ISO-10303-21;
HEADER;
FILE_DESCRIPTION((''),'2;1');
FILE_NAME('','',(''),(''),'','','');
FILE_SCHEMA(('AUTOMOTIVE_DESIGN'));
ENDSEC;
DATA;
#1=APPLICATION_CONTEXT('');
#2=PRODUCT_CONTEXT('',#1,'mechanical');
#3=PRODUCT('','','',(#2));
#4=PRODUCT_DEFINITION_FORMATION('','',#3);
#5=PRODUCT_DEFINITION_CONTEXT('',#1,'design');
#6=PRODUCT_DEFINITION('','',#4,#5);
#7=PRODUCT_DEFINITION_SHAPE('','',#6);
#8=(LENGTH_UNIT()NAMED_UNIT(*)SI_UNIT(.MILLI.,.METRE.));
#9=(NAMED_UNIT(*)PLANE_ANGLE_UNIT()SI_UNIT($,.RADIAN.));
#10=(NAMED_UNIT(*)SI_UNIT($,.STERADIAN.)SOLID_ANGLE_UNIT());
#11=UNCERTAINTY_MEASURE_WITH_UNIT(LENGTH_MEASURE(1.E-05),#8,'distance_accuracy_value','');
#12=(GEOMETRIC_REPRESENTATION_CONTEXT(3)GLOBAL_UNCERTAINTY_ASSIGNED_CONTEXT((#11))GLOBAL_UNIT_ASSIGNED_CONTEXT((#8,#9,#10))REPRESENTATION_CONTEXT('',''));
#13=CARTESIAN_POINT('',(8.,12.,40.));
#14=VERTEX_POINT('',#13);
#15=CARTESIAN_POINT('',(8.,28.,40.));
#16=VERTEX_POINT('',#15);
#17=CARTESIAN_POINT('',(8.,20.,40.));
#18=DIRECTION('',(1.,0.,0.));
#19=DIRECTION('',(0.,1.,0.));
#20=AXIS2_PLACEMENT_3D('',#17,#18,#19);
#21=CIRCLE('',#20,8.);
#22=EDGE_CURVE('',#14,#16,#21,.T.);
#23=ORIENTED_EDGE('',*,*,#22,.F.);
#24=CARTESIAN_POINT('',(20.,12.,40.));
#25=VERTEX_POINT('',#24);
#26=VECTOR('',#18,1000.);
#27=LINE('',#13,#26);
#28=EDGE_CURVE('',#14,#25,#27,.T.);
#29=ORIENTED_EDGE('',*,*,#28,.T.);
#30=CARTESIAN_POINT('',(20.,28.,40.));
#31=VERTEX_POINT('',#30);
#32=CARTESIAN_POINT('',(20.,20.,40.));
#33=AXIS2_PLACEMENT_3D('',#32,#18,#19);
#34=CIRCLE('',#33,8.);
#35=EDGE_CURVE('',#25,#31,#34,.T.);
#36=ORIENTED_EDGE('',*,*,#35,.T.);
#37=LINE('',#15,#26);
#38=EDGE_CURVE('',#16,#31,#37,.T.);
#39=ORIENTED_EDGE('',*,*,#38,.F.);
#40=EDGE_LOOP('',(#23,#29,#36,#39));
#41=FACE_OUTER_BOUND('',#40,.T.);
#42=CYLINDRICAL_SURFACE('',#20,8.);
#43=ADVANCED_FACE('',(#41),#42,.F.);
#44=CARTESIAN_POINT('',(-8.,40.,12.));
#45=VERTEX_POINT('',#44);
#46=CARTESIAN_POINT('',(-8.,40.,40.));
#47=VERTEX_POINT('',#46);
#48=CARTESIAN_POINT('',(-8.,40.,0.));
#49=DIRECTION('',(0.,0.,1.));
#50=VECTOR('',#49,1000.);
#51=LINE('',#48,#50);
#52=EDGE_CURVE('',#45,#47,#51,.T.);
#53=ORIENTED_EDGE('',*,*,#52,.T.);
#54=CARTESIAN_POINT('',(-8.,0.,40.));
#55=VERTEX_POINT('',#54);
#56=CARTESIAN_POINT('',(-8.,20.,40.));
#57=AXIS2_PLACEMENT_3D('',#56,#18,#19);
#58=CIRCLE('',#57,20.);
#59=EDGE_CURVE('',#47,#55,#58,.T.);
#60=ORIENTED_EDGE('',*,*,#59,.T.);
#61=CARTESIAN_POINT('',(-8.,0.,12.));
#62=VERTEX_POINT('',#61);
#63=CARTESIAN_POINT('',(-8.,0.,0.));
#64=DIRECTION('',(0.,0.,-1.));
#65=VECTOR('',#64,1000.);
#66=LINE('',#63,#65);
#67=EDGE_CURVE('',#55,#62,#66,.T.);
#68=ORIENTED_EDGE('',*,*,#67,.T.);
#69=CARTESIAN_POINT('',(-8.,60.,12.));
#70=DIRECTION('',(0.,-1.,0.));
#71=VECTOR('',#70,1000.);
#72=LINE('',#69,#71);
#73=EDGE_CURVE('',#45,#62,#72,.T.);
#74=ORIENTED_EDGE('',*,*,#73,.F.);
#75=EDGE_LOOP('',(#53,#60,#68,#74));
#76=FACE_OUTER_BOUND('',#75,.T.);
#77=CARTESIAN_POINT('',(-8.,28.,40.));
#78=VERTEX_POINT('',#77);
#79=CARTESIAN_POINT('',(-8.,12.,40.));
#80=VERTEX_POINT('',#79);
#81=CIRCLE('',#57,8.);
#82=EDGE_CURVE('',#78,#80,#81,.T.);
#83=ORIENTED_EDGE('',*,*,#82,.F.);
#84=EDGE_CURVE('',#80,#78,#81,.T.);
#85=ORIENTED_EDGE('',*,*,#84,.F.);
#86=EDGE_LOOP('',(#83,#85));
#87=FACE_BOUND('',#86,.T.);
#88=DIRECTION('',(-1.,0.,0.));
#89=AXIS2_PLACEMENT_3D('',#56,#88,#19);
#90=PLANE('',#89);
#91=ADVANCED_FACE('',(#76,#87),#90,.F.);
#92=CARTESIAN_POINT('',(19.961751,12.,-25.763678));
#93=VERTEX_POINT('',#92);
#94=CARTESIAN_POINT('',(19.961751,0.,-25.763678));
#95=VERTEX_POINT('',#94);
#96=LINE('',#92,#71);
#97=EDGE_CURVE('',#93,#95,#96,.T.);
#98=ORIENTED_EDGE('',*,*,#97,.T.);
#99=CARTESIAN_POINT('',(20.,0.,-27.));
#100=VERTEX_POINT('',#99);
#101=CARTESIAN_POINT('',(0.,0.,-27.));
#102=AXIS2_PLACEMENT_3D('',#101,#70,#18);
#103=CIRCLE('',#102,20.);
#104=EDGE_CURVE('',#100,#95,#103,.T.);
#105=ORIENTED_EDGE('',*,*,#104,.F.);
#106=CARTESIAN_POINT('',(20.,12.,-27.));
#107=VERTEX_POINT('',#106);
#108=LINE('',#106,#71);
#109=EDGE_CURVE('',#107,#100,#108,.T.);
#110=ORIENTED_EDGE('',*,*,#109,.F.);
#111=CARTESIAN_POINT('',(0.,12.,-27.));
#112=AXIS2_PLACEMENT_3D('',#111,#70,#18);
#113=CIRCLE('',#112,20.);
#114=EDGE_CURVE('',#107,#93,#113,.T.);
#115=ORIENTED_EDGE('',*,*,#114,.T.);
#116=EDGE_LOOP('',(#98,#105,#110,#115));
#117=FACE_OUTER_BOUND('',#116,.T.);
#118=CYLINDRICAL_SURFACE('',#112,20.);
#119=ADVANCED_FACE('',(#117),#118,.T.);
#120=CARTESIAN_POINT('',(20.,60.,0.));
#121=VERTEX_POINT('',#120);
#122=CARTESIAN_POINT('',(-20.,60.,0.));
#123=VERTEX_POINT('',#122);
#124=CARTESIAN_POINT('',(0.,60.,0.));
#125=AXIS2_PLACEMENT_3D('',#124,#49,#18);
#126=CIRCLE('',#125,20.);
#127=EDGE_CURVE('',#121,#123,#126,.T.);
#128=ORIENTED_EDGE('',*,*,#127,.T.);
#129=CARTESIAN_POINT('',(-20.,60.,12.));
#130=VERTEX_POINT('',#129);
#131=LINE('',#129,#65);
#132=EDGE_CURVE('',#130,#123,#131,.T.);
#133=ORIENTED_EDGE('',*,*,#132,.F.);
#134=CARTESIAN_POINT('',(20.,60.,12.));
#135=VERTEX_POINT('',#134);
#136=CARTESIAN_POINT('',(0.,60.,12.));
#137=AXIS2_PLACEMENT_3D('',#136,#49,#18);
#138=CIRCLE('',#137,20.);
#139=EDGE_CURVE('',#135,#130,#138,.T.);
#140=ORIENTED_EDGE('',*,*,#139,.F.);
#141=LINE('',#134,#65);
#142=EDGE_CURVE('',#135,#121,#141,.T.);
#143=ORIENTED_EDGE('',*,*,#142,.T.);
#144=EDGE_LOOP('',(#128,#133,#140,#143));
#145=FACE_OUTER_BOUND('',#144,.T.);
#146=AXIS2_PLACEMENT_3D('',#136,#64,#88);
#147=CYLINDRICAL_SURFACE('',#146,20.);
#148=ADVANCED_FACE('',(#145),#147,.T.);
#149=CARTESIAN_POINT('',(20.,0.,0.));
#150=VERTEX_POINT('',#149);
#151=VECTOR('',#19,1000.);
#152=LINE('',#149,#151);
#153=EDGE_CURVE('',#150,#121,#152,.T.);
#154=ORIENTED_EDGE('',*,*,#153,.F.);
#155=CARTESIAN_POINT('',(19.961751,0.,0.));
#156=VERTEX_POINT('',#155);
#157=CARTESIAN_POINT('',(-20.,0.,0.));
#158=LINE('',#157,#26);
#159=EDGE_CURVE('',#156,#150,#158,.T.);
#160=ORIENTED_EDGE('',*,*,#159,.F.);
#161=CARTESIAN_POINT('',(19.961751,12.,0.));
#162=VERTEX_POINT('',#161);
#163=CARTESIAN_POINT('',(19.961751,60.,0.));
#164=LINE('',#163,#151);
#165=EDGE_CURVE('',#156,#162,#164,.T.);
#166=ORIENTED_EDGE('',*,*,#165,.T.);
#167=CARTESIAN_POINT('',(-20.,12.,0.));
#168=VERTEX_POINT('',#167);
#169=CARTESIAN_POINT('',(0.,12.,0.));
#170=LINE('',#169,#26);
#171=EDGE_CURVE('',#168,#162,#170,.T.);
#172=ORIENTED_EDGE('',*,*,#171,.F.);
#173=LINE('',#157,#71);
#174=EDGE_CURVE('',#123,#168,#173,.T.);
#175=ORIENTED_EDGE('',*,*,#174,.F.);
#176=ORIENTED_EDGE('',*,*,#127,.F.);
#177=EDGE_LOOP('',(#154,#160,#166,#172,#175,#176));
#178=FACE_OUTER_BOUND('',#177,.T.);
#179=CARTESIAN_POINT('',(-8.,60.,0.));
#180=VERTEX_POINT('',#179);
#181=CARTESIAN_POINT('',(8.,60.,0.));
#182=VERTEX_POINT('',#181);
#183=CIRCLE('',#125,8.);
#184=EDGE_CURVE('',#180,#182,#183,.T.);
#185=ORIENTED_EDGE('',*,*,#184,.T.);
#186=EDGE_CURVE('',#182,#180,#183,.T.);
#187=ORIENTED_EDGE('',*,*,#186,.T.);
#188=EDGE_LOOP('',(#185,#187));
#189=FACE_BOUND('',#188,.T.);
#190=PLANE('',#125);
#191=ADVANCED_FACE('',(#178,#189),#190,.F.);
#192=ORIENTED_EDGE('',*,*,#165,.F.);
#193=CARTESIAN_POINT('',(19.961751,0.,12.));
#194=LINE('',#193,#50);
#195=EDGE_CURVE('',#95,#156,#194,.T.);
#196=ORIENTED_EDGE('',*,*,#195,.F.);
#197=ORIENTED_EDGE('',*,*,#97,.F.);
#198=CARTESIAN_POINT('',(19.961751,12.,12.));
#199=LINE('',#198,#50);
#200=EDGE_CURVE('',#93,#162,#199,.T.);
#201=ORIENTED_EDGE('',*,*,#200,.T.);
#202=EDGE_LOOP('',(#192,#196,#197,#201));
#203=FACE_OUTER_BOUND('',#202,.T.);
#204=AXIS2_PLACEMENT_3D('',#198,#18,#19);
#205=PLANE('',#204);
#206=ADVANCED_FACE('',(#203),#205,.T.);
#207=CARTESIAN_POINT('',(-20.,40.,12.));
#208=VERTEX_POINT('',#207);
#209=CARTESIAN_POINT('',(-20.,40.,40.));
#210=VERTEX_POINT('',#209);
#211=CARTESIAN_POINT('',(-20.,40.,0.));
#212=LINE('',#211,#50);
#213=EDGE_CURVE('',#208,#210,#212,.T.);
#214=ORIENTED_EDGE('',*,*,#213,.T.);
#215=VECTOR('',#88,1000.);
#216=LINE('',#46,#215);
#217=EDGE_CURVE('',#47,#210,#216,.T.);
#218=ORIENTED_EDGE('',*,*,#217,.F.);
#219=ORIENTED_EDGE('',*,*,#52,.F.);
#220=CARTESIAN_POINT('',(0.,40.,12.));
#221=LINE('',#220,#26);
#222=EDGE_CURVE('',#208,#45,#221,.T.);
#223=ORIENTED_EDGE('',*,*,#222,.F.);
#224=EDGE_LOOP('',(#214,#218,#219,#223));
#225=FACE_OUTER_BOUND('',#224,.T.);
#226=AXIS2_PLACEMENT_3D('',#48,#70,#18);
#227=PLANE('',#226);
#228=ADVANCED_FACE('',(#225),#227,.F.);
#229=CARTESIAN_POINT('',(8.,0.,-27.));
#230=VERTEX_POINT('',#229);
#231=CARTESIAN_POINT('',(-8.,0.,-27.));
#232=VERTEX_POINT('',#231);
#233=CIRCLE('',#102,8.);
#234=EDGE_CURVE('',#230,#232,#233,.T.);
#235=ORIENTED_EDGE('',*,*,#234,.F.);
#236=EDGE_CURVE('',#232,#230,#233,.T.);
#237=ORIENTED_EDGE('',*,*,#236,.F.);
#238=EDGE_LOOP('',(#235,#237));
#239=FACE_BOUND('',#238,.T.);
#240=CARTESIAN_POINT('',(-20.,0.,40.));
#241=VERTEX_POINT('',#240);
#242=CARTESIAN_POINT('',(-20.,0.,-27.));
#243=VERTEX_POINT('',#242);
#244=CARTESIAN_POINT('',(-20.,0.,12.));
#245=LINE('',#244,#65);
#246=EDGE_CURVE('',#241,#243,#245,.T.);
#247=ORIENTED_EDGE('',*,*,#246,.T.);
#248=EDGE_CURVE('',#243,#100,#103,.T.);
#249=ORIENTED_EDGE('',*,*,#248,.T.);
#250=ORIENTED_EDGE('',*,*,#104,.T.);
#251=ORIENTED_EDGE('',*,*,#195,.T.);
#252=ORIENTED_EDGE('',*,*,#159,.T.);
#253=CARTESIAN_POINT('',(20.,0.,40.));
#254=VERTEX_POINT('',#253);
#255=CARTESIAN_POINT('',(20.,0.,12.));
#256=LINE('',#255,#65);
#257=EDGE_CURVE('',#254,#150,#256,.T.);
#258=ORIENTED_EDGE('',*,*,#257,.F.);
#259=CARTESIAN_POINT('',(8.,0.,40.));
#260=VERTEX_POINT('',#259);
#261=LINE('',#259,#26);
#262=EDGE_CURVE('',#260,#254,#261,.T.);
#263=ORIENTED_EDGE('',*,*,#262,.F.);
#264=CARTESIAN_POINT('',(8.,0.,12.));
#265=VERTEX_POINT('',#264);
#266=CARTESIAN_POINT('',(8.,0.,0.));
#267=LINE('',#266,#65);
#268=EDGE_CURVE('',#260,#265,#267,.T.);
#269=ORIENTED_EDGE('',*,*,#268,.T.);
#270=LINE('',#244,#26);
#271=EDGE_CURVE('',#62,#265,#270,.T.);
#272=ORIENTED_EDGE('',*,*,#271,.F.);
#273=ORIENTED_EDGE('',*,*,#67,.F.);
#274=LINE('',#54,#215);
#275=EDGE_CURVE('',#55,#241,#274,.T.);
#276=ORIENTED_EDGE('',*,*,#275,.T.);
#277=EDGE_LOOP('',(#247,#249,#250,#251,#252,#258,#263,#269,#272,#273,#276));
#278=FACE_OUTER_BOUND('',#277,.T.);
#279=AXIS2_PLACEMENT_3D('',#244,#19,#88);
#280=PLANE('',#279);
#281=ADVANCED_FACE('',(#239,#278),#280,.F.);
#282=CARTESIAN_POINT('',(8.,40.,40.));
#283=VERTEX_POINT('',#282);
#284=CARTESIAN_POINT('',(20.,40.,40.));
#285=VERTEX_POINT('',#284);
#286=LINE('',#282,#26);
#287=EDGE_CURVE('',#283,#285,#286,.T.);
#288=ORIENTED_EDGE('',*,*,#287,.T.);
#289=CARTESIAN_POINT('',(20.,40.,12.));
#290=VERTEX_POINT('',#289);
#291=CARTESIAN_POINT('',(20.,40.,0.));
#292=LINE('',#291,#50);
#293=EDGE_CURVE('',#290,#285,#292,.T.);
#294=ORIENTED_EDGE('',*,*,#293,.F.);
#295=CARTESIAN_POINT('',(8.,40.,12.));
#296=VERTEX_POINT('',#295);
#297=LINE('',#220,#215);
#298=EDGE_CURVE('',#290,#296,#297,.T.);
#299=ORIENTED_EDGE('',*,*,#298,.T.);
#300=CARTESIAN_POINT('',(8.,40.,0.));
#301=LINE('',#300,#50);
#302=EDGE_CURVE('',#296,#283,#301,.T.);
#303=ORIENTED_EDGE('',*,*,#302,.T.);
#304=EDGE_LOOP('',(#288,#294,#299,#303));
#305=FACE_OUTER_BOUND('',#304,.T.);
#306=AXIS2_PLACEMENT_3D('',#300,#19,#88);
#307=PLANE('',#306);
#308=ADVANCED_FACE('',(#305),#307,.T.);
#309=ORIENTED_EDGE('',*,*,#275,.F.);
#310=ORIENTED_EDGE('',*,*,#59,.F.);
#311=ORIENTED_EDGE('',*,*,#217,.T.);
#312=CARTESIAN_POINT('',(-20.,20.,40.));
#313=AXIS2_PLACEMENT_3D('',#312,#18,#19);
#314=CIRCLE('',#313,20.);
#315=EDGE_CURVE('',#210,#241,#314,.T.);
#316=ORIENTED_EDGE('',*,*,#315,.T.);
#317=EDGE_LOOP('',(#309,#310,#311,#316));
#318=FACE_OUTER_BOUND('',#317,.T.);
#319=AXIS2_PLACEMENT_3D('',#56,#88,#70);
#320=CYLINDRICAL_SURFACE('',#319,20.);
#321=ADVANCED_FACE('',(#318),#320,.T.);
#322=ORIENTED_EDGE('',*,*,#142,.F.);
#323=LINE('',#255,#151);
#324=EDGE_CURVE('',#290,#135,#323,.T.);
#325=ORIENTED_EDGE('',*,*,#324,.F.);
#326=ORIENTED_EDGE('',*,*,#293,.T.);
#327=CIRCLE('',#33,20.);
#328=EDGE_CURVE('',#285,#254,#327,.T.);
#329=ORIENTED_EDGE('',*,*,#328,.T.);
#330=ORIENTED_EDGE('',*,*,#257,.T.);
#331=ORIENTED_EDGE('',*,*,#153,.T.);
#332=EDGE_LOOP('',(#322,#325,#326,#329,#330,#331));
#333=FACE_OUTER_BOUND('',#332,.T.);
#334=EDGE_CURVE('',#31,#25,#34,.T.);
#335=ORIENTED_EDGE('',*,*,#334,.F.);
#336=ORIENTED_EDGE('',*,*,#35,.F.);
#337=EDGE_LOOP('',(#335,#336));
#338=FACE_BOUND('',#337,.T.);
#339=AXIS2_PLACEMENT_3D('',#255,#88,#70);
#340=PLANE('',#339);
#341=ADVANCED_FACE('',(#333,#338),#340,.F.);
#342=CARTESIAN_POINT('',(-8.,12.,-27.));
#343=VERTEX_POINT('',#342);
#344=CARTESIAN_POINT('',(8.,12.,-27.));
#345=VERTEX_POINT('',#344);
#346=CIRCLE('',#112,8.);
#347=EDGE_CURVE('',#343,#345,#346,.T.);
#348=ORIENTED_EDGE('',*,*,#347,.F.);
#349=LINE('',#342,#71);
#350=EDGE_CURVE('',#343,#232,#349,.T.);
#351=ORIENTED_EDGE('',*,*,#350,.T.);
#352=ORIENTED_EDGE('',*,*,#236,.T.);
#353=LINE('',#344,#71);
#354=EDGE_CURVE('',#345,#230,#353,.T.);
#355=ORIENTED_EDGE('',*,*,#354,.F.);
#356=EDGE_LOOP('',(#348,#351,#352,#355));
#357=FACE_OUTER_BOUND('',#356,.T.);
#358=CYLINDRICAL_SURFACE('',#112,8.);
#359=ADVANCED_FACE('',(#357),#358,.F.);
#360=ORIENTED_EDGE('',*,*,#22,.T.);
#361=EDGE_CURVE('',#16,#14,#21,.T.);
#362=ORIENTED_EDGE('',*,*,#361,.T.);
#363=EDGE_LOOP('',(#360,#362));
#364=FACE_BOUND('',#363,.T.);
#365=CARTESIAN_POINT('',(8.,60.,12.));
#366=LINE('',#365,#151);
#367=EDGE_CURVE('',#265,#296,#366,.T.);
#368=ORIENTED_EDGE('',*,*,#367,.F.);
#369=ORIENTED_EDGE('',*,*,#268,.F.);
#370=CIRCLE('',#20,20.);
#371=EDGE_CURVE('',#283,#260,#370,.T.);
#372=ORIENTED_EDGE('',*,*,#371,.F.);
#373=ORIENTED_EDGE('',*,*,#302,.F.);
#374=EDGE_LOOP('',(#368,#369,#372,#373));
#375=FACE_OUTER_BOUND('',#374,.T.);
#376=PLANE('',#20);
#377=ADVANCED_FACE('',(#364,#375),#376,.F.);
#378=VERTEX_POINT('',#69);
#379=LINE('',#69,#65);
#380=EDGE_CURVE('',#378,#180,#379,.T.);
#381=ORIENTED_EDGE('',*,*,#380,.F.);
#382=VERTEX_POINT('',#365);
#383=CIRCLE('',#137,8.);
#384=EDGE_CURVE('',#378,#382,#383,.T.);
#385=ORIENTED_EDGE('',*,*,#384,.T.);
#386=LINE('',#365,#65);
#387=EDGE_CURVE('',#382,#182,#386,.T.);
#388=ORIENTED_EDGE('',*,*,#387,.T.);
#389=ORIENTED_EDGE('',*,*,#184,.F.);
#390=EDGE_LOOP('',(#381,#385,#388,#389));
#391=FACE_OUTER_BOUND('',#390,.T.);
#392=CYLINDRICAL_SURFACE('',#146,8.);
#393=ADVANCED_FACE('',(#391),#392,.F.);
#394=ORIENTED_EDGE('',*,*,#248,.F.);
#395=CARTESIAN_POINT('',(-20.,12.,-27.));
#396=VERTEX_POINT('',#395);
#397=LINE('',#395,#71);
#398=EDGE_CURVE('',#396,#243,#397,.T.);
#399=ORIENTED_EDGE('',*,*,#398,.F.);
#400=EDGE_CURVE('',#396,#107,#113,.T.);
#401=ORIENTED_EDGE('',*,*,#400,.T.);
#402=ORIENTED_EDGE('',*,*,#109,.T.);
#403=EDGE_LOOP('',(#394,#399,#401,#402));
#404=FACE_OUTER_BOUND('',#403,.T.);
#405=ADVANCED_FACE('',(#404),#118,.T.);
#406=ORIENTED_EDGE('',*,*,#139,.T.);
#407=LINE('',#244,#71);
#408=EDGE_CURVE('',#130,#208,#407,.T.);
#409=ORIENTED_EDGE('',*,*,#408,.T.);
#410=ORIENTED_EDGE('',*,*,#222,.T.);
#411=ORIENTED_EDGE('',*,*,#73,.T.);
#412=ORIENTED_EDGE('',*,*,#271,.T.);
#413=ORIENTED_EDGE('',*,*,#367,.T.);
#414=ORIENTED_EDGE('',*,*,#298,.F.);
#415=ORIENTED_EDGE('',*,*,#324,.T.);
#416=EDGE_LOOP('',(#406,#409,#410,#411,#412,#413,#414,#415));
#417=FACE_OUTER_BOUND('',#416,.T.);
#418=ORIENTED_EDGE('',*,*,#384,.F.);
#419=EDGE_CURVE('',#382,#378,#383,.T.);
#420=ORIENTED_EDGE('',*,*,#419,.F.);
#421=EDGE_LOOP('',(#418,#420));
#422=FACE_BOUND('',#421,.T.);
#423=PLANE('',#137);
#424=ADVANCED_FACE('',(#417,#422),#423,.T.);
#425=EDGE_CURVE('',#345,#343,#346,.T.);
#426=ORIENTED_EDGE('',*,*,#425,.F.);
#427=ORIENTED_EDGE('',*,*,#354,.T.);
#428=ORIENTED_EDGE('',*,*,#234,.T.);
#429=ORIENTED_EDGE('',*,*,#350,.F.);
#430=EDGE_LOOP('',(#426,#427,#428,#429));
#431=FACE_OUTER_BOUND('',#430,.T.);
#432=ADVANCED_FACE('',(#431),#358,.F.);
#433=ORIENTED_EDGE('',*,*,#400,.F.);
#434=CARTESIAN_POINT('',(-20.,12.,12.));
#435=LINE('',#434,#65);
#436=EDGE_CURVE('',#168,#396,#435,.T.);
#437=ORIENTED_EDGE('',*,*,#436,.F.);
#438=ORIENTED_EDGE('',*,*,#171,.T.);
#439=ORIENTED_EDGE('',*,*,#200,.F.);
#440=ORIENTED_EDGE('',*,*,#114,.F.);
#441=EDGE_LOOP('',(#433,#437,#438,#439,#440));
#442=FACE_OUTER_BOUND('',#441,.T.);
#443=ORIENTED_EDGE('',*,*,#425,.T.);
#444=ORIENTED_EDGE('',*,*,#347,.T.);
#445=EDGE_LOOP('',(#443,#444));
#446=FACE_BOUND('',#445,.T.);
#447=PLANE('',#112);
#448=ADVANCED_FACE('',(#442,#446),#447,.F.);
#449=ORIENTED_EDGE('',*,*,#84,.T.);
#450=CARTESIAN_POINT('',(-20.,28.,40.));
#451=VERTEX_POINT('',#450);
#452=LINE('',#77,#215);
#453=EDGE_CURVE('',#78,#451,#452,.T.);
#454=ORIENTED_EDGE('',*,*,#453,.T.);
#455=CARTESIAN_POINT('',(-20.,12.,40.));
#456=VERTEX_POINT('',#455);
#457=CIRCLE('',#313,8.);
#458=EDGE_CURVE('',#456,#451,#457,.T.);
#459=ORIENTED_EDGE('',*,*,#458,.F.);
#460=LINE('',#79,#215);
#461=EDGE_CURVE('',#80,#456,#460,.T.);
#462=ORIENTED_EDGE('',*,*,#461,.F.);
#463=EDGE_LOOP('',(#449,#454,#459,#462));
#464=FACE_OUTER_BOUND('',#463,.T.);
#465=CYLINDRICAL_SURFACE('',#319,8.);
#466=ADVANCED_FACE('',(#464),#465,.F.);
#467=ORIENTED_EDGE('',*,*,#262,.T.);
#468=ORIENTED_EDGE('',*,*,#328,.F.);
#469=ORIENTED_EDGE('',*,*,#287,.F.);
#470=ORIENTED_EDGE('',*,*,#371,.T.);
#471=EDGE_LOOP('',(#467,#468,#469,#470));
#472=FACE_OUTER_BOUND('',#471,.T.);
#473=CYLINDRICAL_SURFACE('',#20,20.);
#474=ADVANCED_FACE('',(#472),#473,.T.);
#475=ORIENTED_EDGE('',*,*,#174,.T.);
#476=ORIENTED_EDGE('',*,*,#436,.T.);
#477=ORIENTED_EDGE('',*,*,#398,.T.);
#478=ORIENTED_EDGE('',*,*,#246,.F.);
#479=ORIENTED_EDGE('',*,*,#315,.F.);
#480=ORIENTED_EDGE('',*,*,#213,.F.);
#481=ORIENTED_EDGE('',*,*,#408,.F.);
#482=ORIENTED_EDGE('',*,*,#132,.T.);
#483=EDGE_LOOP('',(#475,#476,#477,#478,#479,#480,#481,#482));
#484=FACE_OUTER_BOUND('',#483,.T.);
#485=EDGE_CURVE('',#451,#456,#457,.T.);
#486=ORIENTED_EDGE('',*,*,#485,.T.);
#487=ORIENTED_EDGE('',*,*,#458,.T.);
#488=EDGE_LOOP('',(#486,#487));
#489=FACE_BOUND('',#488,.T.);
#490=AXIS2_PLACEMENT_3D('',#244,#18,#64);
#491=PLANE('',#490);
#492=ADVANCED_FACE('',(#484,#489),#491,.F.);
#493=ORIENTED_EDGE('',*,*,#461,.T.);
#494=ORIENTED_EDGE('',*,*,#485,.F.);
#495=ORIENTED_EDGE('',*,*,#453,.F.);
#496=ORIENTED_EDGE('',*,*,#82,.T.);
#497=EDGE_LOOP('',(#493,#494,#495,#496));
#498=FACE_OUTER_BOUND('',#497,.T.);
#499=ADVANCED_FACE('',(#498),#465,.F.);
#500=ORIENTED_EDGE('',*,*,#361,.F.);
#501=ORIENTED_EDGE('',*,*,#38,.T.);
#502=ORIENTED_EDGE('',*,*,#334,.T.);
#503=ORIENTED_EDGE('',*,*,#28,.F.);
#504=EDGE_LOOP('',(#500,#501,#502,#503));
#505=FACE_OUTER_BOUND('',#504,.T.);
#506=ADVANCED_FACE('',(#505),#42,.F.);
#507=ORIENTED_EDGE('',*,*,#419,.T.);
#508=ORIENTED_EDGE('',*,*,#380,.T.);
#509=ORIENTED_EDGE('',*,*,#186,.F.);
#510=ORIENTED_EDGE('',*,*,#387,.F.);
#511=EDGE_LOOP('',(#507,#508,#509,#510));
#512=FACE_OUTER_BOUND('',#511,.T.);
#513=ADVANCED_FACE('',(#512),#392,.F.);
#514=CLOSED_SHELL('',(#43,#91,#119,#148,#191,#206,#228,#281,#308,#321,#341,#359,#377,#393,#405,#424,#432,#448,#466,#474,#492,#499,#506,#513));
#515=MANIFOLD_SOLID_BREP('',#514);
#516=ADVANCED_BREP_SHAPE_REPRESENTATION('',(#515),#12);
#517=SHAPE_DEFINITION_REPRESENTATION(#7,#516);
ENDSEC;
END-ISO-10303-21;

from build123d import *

# Parameters (mm, degrees)
UPRIGHT_LUG_SKETCH_R     = 8
UPRIGHT_LUG_DEPTH        = 12
CLEVIS_SIDE_LUG_SKETCH_R = 8
CLEVIS_SIDE_LUG_DEPTH    = 12
HORIZONTAL_LUG_SKETCH_R  = 8
HORIZONTAL_LUG_DEPTH     = 12


with BuildPart() as part:
    # Upright Lug Sketch → Upright Lug (new body)
    with BuildSketch(Plane.XY):
        with BuildLine():
            Line((-20, 0), (20, 0))
            Line((20, 0), (20, 60))
            ThreePointArc((20, 60), (0, 80), (-20, 60))
            Line((-20, 60), (-20, 0))
        make_face()
        with Locations((0, 60)):
            Circle(UPRIGHT_LUG_SKETCH_R, mode=Mode.SUBTRACT)
    extrude(amount=UPRIGHT_LUG_DEPTH)

    # Clevis Side Lug Sketch → Clevis Side Lug (add)
    with BuildSketch(Plane(origin=(20, 0, 0), x_dir=(0, 0, -1), z_dir=(1, 0, 0))):
        with BuildLine():
            Line((0, 0), (-40, 0))
            ThreePointArc((-40, 0), (-60, 20), (-40, 40))
            Line((-40, 40), (0, 40))
            Line((0, 40), (0, 0))
        make_face()
        with Locations(Location((-40, 20, 0), (0, 0, 90))):
            Circle(CLEVIS_SIDE_LUG_SKETCH_R, mode=Mode.SUBTRACT)
    clevis_side_lug = extrude(amount=-CLEVIS_SIDE_LUG_DEPTH)

    # Clevis Side Lug Mirror: Clevis Side Lug across plane
    add(clevis_side_lug.mirror(Plane(origin=(0, 0, 0), x_dir=(0, 0, 1), z_dir=(1, 0, 0))))

    # Horizontal Lug Sketch → Horizontal Lug (add)
    with BuildSketch(Plane.XZ):
        with BuildLine():
            Line((-20, 12), (19.961751116, 12))
            Line((19.961751116, 12), (19.961751116, -25.763677886))
            ThreePointArc((19.961751116, -25.763677886), (0.618456819, -46.990435492), (-20, -27))
            Line((-20, -27), (-20, 12))
        make_face()
        with Locations((0, -27)):
            Circle(HORIZONTAL_LUG_SKETCH_R, mode=Mode.SUBTRACT)
    extrude(amount=-HORIZONTAL_LUG_DEPTH)


solid = part.part
